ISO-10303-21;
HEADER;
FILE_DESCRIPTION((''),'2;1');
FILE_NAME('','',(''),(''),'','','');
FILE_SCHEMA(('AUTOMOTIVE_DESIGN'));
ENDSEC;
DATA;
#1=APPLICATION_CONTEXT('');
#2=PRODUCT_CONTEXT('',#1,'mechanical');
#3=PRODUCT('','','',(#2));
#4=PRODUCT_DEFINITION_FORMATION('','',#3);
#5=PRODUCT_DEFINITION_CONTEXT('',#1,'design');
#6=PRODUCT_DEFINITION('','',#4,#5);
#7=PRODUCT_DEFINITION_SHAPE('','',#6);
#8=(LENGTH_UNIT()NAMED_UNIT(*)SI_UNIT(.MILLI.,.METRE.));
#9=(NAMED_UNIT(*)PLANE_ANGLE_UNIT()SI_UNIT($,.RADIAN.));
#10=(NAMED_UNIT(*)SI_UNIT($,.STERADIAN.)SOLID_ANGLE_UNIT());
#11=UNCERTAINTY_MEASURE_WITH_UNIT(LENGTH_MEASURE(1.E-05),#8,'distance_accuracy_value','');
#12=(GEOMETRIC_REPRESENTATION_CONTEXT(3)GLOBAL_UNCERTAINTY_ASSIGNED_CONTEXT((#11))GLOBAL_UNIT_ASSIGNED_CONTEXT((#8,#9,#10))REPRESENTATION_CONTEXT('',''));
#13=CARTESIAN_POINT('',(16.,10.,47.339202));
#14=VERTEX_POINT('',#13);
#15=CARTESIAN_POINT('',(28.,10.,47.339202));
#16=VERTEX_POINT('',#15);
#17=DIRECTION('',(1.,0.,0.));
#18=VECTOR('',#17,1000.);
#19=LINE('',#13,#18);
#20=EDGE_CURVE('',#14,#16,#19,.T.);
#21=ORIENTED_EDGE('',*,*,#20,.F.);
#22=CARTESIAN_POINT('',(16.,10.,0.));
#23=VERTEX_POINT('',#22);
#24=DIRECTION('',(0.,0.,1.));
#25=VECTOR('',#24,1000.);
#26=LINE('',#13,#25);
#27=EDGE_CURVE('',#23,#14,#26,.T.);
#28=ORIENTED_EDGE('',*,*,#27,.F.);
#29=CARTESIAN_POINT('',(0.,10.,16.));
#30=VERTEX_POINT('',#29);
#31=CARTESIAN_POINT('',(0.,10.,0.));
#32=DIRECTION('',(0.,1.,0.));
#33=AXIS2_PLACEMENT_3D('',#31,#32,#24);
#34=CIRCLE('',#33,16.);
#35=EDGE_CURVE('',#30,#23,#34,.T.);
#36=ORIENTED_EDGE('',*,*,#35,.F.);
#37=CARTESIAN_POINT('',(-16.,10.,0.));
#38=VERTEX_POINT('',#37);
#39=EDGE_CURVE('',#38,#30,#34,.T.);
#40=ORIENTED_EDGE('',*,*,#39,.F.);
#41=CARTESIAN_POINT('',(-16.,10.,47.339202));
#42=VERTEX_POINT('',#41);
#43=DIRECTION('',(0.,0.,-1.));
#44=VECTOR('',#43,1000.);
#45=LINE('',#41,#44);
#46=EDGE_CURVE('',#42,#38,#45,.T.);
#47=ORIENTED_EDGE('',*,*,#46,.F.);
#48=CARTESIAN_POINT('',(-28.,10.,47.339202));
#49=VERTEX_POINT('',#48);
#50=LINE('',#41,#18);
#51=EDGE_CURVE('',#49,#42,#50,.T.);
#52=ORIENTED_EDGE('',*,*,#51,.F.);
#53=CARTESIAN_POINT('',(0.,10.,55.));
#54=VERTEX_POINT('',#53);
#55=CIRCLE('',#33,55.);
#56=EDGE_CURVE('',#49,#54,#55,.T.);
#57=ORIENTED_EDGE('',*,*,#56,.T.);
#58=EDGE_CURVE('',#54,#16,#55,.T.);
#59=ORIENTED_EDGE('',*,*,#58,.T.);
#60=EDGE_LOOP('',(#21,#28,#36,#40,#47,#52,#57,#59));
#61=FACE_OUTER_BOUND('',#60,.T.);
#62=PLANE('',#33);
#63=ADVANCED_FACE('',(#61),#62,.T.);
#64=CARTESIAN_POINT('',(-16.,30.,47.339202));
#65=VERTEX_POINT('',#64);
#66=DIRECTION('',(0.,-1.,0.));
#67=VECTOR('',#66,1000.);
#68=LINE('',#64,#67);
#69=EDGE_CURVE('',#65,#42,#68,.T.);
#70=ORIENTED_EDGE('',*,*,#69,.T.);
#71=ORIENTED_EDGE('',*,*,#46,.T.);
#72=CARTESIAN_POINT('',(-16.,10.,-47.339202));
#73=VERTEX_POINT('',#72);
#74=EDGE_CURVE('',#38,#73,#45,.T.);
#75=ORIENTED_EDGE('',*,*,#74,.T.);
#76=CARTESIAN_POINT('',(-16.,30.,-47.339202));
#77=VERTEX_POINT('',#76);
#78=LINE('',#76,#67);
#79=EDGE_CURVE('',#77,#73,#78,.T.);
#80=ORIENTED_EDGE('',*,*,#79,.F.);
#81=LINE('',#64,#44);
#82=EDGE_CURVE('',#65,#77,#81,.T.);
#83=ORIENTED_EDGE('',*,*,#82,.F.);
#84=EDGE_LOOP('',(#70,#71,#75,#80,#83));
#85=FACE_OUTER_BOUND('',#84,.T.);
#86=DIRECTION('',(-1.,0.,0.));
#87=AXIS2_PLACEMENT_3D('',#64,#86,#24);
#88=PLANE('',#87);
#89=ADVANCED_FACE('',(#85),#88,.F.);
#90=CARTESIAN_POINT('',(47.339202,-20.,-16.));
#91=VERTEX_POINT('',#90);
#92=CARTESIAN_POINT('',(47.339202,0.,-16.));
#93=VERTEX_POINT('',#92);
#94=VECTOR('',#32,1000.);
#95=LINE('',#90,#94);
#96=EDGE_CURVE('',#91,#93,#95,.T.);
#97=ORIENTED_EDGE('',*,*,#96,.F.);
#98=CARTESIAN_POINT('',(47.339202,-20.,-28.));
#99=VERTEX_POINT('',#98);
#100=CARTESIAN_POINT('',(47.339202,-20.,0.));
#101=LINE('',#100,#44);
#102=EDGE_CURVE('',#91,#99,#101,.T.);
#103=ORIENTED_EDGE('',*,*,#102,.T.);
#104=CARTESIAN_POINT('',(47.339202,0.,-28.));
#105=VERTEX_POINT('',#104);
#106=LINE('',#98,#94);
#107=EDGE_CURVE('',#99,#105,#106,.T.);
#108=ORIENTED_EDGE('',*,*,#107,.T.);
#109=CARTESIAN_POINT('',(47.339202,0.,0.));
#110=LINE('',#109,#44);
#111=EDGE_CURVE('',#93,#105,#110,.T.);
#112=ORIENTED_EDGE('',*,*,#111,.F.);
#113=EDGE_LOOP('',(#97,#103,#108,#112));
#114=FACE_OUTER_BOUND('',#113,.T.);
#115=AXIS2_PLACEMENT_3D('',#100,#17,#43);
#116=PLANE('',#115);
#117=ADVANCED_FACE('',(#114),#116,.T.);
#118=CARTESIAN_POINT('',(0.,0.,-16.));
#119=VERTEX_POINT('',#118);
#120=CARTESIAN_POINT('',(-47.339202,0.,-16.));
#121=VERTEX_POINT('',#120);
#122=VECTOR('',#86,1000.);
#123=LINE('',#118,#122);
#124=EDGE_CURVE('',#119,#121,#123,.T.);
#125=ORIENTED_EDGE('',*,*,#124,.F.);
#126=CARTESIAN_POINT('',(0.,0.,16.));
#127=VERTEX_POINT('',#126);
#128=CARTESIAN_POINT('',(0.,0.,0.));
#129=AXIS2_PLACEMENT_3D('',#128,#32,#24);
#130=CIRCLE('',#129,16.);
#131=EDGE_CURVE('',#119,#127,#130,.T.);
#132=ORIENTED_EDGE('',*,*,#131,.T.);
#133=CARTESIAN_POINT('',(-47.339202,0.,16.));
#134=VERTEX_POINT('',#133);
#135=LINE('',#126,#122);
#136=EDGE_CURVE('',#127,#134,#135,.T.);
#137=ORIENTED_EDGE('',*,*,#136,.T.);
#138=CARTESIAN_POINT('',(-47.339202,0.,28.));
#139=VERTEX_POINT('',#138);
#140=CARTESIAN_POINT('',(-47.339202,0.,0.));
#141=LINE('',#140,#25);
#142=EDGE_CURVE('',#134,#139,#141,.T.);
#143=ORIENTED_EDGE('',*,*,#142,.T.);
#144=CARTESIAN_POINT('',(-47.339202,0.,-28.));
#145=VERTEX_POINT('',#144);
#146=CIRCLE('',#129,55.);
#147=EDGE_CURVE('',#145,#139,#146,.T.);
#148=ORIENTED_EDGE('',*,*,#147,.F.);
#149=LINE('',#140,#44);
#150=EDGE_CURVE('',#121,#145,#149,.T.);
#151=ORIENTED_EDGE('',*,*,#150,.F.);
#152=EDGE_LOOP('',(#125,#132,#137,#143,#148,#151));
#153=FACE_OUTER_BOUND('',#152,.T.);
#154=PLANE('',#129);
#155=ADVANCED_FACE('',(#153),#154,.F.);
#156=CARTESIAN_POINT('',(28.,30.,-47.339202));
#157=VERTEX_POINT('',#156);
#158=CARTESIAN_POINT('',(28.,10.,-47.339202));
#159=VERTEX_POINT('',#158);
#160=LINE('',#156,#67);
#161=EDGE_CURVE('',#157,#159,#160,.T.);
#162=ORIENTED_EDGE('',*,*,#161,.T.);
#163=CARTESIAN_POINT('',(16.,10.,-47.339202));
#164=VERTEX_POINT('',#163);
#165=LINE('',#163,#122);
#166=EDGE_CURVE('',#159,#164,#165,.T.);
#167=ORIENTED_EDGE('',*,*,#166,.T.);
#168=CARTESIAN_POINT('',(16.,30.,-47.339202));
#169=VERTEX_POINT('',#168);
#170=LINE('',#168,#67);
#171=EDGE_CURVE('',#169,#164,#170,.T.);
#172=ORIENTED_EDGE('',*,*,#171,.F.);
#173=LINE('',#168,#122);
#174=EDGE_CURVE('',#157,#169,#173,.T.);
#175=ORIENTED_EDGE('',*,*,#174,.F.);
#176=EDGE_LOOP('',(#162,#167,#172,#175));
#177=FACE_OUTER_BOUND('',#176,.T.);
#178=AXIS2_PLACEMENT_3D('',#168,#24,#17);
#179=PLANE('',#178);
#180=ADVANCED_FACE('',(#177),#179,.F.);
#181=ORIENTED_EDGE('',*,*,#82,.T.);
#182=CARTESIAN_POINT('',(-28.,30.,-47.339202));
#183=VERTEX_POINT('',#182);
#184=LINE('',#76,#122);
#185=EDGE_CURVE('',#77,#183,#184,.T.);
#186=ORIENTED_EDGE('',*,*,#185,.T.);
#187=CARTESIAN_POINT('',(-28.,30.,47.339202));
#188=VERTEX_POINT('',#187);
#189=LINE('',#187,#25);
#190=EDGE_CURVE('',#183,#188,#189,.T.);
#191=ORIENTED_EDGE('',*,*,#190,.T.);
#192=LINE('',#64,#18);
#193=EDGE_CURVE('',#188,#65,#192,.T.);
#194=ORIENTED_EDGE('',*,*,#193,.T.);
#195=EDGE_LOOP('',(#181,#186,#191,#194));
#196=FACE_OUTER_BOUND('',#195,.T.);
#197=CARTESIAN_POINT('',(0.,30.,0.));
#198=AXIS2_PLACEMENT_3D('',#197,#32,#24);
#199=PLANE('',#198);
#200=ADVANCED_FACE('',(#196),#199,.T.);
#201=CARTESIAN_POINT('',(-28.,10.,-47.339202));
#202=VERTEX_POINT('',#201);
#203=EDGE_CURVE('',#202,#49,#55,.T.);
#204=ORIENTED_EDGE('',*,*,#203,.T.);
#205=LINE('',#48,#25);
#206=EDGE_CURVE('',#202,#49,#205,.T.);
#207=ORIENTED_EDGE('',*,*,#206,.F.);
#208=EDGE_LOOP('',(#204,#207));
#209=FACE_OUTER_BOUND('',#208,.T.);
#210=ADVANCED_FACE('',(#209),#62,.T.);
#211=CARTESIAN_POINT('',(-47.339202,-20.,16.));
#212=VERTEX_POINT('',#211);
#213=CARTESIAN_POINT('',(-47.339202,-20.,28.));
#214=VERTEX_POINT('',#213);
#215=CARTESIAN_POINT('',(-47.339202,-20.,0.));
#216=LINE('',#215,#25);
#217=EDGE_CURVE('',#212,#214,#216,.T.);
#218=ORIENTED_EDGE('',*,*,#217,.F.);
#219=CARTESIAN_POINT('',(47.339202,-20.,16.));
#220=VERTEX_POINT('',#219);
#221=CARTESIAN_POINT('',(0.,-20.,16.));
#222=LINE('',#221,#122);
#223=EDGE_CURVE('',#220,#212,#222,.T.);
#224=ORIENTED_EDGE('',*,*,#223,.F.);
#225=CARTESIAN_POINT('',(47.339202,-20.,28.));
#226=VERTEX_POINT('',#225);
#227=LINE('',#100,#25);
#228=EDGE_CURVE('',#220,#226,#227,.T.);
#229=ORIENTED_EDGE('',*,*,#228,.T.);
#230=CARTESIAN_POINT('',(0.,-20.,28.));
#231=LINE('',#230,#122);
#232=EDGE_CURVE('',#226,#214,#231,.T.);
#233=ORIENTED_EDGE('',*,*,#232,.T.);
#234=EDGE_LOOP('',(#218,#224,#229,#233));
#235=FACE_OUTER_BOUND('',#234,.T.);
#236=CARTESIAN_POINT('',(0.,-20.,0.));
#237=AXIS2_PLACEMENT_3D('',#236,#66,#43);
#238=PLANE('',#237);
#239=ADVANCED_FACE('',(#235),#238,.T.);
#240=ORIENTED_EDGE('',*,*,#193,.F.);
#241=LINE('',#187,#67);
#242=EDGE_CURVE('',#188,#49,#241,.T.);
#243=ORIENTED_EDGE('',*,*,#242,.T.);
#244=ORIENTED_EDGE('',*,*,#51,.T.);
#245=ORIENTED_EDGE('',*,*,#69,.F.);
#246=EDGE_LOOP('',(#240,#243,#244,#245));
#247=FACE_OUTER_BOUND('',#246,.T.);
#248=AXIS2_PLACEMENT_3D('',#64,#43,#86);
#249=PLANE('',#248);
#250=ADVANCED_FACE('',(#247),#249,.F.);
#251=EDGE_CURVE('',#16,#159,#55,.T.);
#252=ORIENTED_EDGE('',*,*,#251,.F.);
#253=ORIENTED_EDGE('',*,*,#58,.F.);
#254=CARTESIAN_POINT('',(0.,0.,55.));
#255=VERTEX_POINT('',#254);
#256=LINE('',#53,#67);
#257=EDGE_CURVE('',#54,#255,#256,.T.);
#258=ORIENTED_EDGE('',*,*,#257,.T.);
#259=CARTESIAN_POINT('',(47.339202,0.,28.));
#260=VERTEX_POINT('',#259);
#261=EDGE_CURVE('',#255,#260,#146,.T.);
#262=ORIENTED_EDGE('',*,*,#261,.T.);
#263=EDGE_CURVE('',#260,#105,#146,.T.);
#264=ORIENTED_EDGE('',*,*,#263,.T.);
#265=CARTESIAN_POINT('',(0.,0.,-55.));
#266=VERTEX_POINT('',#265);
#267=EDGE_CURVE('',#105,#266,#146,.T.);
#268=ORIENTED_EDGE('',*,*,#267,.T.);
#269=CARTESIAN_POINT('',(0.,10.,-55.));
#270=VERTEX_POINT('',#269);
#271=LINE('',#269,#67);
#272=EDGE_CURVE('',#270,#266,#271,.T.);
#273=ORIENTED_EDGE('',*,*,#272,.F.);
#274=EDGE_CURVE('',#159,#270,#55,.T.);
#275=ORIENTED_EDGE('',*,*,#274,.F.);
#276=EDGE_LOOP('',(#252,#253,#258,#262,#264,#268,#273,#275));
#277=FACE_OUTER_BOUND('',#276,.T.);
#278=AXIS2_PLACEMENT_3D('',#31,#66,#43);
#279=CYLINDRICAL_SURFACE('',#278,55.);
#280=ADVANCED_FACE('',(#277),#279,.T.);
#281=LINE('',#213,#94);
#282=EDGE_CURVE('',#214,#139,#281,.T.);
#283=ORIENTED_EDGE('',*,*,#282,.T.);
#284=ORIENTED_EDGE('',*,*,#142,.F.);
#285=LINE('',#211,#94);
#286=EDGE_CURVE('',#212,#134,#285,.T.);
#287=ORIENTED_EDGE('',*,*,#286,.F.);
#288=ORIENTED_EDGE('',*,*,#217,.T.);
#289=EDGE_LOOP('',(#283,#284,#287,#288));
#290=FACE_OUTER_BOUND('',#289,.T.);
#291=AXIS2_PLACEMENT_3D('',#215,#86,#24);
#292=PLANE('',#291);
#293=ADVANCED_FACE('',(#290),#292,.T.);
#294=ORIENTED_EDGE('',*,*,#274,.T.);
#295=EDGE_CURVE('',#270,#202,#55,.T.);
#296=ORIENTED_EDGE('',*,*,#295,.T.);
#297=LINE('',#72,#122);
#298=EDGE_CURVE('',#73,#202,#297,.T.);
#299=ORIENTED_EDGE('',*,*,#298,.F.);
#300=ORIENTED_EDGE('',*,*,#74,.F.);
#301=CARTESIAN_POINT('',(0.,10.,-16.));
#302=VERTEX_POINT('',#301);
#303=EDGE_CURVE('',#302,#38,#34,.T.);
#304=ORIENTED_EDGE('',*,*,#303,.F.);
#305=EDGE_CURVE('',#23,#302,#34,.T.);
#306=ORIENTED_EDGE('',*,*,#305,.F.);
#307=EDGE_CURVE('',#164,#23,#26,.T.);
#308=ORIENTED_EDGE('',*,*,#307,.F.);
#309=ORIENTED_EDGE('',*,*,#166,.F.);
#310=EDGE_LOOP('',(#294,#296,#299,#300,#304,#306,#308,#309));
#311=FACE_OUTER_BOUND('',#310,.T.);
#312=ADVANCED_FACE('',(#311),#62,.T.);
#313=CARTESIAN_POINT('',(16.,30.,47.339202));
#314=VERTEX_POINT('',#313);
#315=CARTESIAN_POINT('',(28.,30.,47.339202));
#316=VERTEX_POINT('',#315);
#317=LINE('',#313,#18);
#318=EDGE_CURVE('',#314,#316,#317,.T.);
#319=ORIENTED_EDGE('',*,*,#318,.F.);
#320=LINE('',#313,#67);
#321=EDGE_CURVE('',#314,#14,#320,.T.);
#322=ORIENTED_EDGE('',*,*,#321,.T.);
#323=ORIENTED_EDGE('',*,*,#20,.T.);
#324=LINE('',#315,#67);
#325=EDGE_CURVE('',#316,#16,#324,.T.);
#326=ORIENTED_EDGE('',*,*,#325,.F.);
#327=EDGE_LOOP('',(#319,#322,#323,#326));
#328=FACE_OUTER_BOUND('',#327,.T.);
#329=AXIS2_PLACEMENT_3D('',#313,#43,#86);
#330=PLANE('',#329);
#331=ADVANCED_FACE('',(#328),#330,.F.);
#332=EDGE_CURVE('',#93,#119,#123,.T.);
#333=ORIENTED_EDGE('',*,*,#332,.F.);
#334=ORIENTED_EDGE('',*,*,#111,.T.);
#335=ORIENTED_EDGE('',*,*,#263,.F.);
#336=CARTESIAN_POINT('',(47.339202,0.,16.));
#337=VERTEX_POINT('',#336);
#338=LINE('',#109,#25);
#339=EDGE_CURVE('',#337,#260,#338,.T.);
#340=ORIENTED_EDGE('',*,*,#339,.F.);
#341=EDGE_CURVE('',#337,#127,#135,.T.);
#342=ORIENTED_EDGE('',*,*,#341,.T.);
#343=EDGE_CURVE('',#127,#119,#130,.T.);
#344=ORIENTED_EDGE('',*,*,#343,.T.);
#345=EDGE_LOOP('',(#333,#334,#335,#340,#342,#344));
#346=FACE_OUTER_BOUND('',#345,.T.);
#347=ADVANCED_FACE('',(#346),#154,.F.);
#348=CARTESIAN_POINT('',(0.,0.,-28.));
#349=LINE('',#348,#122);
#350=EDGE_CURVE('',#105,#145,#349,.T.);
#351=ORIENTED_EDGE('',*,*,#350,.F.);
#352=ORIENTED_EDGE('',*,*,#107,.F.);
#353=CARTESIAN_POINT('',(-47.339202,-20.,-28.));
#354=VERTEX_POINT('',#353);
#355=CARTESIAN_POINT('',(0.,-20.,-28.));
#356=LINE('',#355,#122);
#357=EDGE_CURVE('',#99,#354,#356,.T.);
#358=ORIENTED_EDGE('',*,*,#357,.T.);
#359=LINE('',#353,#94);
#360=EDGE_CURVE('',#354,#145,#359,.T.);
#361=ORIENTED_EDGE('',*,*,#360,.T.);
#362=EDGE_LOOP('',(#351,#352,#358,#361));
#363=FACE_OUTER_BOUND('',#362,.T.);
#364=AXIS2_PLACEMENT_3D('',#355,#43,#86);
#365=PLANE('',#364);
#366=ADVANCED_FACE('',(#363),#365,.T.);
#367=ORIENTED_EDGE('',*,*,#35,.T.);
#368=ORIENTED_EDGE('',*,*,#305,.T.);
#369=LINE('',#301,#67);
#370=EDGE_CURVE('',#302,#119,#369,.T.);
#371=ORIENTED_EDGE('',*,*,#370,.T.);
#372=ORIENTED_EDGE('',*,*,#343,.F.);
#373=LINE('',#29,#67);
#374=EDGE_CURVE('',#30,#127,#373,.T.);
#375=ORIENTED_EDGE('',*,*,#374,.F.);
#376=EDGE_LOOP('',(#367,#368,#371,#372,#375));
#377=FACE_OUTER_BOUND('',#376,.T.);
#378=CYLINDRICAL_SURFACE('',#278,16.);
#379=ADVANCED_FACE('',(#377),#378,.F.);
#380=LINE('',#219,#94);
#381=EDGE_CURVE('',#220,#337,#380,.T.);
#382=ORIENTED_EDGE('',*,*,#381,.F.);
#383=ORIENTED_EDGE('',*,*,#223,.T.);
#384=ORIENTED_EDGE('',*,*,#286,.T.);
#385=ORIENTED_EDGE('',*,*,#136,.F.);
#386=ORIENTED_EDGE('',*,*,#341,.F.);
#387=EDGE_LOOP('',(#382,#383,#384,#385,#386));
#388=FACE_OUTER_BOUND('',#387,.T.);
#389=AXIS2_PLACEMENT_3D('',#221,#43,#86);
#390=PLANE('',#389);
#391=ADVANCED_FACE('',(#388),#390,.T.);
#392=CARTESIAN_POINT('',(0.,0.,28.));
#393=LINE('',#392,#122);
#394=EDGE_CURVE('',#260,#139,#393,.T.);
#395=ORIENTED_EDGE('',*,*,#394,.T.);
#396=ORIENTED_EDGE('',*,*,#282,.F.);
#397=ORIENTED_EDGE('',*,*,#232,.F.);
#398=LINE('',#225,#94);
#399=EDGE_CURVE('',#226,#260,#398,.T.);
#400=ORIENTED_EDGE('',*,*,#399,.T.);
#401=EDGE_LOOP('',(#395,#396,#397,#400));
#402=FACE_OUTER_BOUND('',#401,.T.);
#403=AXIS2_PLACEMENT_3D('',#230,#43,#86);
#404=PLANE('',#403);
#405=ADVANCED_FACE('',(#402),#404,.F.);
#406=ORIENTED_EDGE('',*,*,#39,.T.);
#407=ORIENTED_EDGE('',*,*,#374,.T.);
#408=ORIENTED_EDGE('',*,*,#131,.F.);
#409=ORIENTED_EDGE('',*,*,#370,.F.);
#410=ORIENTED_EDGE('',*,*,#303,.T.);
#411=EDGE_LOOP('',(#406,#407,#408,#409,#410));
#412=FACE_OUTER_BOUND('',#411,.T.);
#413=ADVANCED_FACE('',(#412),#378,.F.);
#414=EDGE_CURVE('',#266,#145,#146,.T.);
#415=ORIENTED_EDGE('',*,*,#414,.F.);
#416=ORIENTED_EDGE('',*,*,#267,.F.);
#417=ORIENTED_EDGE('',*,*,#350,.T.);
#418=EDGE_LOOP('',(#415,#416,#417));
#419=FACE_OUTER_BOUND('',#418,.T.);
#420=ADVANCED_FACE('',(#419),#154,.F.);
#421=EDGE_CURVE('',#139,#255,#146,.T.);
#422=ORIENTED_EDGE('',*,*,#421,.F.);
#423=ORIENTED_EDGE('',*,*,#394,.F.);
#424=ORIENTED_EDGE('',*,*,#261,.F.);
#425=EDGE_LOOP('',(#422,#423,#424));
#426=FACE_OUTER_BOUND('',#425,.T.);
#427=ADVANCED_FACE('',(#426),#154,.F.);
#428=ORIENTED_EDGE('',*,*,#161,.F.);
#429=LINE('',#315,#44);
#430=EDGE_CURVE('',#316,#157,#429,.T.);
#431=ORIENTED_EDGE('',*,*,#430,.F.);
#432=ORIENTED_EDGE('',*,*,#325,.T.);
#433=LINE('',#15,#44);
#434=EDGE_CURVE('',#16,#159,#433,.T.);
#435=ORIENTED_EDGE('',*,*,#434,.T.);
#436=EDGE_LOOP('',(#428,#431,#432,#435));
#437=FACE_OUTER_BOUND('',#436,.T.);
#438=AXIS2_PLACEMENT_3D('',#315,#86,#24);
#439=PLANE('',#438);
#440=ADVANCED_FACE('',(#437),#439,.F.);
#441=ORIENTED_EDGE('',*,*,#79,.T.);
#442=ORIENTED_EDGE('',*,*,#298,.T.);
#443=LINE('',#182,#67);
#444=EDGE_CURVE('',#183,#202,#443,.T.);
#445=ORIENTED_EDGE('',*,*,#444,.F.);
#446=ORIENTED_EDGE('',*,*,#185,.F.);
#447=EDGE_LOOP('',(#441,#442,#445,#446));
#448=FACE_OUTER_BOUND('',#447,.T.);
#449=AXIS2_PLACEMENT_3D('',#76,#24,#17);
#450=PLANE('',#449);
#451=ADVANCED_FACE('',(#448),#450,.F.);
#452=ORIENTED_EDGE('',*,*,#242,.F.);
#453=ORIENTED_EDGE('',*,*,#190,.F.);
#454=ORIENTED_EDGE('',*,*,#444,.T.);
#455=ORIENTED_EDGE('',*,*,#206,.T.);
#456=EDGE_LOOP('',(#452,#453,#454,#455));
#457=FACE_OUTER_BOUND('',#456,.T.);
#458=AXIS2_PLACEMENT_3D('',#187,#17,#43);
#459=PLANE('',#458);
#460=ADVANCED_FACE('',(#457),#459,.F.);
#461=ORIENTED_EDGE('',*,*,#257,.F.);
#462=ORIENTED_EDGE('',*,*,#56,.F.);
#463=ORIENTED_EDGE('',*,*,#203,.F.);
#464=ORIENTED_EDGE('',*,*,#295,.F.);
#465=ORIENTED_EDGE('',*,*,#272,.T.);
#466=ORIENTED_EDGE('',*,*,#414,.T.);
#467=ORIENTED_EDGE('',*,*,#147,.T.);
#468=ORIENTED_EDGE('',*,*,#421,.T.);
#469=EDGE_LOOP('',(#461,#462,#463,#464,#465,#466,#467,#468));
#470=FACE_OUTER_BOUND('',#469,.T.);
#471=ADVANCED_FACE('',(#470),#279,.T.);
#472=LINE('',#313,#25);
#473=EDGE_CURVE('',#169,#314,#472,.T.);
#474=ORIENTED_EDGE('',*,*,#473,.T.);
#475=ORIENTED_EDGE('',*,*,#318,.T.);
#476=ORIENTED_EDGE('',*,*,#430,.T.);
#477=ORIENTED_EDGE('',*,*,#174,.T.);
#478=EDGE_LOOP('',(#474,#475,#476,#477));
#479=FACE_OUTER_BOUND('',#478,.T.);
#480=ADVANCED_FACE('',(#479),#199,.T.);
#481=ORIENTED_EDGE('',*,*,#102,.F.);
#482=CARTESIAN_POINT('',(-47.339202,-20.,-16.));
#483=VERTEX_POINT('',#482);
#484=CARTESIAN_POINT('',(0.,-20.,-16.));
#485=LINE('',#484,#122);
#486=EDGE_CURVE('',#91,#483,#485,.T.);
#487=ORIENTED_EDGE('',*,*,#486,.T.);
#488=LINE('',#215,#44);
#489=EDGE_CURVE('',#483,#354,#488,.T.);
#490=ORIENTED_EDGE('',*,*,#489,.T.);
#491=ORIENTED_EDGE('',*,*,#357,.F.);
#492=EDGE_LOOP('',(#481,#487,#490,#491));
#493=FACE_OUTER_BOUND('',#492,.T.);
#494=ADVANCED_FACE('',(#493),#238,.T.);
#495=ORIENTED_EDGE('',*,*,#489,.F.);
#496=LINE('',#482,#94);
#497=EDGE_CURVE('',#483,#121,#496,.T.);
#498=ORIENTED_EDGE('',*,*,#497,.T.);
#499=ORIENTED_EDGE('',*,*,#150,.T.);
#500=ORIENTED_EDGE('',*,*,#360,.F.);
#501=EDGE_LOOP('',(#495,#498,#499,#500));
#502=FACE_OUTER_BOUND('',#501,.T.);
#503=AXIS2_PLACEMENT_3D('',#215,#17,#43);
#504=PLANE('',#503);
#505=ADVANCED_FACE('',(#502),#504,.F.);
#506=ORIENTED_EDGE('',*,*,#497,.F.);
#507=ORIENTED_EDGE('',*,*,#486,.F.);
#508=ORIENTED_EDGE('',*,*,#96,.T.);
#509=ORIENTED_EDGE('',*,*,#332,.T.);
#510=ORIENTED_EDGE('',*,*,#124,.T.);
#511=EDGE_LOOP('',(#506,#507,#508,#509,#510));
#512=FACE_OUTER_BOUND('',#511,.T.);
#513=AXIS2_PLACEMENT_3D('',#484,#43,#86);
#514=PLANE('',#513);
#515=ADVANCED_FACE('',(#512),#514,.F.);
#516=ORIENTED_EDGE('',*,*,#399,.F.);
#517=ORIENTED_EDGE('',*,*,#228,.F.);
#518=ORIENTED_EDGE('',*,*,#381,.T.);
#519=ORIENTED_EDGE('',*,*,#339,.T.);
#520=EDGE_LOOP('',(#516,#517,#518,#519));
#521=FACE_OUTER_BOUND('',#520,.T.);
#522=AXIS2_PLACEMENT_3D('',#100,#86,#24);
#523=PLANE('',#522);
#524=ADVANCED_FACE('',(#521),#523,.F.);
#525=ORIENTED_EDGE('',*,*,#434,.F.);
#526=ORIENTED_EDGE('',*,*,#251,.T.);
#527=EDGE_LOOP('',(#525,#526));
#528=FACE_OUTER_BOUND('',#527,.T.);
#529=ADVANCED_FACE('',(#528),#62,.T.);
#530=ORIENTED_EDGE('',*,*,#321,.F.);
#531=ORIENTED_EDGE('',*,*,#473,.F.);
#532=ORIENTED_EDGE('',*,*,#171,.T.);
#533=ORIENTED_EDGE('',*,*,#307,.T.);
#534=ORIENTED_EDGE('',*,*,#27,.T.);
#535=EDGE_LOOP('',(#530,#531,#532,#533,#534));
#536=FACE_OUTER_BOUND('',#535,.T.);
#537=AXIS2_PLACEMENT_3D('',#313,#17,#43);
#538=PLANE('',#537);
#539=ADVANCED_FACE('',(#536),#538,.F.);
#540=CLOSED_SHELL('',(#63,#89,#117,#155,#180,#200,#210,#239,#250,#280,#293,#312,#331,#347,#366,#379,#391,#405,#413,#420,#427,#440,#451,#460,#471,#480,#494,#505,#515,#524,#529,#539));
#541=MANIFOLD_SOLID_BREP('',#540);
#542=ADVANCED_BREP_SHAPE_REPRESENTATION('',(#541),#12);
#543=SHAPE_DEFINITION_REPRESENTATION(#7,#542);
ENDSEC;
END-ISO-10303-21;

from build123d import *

# Parameters (mm, degrees)
BASE_DISC_SKETCH_R          = 55
BASE_DISC_SKETCH_R_2        = 16
BASE_DISC_110_BORE_32_DEPTH = 10
TOP_RAILS_SKETCH_W          = 12
TOP_RAILS_SKETCH_H          = 94.678403028
TOP_RAILS_DEPTH             = 20
BOTTOM_LEGS_SKETCH_W        = 94.678403028
BOTTOM_LEGS_SKETCH_H        = 12
BOTTOM_LEGS_DEPTH           = 20


with BuildPart() as part:
    # Base Disc Sketch → Base Disc Ø110 Bore Ø32 (new body)
    with BuildSketch(Plane(origin=(0, 0, 0), x_dir=(1, 0, 0), z_dir=(0, 1, 0))):
        with Locations(Location((0, 0, 0), (0, 0, 270))):
            Circle(BASE_DISC_SKETCH_R)
        with Locations(Location((0, 0, 0), (0, 0, 270))):
            Circle(BASE_DISC_SKETCH_R_2, mode=Mode.SUBTRACT)
    extrude(amount=BASE_DISC_110_BORE_32_DEPTH)

    # Top Rails Sketch → Top Rails (add)
    with BuildSketch(Plane(origin=(0, 10, 0), x_dir=(1, 0, 0), z_dir=(0, 1, 0))):
        with Locations((22, 0)):
            Rectangle(TOP_RAILS_SKETCH_W, TOP_RAILS_SKETCH_H)
        with Locations((-22, 0)):
            Rectangle(TOP_RAILS_SKETCH_W, TOP_RAILS_SKETCH_H)
    extrude(amount=TOP_RAILS_DEPTH)

    # Bottom Legs Sketch → Bottom Legs (add)
    with BuildSketch(Plane.XZ):
        with Locations((0, 22)):
            Rectangle(BOTTOM_LEGS_SKETCH_W, BOTTOM_LEGS_SKETCH_H)
        with Locations((0, -22)):
            Rectangle(BOTTOM_LEGS_SKETCH_W, BOTTOM_LEGS_SKETCH_H)
    extrude(amount=BOTTOM_LEGS_DEPTH)


solid = part.part
